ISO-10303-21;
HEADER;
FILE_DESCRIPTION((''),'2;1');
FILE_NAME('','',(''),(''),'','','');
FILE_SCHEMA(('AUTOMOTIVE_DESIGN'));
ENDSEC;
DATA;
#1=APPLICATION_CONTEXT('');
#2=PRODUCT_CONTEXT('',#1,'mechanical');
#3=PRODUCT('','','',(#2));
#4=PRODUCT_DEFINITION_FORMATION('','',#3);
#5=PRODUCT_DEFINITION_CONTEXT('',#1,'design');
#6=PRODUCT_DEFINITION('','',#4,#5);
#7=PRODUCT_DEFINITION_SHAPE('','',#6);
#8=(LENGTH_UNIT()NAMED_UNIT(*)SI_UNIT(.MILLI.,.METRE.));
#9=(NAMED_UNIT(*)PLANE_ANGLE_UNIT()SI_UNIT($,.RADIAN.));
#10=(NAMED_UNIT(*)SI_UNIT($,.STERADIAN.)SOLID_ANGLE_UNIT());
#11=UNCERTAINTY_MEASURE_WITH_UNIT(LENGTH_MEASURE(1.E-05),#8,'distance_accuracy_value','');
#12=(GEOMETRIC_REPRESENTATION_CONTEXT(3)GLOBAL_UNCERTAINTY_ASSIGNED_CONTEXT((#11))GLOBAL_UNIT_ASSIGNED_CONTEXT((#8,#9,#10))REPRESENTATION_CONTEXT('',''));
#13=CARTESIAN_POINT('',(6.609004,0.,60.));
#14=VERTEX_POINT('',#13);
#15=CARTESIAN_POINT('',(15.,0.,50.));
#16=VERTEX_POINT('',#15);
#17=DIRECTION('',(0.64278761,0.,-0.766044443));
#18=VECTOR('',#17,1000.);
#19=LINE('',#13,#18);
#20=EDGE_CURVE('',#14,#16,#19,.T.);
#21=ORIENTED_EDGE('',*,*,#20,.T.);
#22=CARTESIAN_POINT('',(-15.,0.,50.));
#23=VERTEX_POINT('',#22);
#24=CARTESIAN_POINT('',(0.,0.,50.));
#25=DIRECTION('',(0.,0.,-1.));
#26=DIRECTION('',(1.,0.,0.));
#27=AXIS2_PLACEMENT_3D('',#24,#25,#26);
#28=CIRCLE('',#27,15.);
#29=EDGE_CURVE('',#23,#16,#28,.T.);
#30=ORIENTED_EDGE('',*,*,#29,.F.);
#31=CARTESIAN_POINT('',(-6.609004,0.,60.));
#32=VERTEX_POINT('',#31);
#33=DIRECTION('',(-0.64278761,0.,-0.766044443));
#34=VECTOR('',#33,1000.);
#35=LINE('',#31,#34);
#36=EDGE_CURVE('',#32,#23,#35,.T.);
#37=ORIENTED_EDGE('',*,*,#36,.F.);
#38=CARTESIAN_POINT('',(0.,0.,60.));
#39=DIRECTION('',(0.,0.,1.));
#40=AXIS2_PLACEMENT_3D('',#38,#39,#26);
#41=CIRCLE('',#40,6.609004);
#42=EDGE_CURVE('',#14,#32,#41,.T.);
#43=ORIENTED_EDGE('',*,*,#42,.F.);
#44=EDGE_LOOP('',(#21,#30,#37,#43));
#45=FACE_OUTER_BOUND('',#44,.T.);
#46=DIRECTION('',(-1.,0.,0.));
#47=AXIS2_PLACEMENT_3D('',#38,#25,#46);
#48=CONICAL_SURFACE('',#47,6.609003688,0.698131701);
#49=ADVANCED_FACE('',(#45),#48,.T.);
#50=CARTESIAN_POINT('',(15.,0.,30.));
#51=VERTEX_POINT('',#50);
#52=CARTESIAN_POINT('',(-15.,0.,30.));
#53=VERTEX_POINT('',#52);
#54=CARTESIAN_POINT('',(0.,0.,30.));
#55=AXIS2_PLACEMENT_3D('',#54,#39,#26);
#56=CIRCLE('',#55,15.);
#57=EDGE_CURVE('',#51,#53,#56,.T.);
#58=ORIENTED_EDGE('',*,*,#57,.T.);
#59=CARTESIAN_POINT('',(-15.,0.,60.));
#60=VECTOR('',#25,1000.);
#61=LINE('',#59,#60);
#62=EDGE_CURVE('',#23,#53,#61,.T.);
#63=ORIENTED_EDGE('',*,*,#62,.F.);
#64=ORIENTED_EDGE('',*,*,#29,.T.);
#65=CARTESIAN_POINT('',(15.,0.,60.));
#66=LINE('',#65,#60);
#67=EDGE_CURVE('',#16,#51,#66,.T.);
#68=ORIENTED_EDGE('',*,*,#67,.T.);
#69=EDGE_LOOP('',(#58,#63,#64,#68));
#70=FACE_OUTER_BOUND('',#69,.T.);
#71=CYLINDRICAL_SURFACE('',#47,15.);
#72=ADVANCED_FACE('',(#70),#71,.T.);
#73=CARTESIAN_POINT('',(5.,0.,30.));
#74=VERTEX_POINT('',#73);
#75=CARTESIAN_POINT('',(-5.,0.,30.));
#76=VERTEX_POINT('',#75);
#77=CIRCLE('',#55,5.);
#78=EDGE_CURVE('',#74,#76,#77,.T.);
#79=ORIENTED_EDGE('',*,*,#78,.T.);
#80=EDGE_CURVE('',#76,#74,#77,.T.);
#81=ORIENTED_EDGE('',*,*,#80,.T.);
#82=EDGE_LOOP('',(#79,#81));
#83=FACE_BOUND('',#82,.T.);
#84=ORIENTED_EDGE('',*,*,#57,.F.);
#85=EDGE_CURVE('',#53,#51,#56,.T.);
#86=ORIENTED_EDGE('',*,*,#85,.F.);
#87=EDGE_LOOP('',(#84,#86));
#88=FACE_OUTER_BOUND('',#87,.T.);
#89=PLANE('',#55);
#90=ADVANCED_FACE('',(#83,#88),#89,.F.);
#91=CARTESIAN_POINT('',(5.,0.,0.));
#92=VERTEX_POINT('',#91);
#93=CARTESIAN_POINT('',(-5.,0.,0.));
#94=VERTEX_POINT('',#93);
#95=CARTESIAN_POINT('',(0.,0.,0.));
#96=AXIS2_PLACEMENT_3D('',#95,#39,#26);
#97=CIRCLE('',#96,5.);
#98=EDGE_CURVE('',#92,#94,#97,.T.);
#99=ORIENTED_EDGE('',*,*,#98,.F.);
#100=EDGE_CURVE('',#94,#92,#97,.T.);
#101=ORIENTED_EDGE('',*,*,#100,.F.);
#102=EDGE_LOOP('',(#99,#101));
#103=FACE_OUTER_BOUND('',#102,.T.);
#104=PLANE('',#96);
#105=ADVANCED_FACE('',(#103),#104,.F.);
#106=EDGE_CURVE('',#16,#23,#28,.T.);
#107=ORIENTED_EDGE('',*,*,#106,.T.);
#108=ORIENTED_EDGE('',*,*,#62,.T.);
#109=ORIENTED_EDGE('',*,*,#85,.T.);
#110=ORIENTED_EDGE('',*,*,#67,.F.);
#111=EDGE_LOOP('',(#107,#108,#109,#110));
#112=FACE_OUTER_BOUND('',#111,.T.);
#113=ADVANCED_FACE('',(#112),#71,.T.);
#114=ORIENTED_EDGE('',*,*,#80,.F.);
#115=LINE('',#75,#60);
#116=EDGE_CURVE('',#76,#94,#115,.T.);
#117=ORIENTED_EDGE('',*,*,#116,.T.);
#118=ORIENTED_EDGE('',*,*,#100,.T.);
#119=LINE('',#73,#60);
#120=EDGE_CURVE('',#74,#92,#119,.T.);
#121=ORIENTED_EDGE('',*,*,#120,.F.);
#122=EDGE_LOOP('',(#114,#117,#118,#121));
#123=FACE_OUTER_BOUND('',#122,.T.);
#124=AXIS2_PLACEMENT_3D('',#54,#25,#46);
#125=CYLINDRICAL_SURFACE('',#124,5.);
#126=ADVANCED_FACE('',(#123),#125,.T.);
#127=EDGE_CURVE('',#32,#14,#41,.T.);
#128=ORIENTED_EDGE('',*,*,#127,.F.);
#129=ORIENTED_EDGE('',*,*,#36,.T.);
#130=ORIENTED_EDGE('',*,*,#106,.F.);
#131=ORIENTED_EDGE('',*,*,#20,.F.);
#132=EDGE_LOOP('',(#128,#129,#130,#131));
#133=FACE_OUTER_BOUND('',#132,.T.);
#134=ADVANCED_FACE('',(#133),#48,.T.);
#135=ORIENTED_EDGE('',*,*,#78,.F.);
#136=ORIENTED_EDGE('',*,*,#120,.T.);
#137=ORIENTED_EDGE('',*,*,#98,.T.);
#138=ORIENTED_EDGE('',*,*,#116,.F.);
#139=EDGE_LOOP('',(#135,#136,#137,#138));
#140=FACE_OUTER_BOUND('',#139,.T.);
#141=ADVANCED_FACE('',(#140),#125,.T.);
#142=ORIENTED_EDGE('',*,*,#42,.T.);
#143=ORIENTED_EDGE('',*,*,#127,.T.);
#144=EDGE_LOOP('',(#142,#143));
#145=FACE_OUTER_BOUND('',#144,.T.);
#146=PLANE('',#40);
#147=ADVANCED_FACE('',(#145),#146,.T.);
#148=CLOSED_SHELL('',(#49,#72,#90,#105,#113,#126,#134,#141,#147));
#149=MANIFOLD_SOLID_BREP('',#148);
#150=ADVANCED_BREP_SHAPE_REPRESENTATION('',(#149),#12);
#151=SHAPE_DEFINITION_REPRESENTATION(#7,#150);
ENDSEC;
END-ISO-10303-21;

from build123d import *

# Parameters (mm, degrees)
SKETCH1_R           = 5
BOSS_EXTRUDE1_DEPTH = 30
SKETCH2_R           = 15
BOSS_EXTRUDE2_DEPTH = 30
CHAMFER1_SIZE       = 10
CHAMFER1_SIZE2      = 8.390996312


with BuildPart() as part:
    # Sketch1 → Boss-Extrude1 (new body)
    with BuildSketch(Plane.XY):
        Circle(SKETCH1_R)
    extrude(amount=BOSS_EXTRUDE1_DEPTH)

    # Sketch2 → Boss-Extrude2 (add)
    with BuildSketch(Plane.XY.offset(30)):
        Circle(SKETCH2_R)
    extrude(amount=BOSS_EXTRUDE2_DEPTH)

    # Chamfer1
    chamfer1_edges = [part.edges().sort_by_distance(p)[0] for p in [
        (-15, 0, 60),
    ]]
    chamfer1_side = [part.faces().sort_by_distance(p)[0] for p in [
        (-15, 0, 45),
    ]]
    chamfer(chamfer1_edges, length=CHAMFER1_SIZE, length2=CHAMFER1_SIZE2, reference=chamfer1_side[0])


solid = part.part
